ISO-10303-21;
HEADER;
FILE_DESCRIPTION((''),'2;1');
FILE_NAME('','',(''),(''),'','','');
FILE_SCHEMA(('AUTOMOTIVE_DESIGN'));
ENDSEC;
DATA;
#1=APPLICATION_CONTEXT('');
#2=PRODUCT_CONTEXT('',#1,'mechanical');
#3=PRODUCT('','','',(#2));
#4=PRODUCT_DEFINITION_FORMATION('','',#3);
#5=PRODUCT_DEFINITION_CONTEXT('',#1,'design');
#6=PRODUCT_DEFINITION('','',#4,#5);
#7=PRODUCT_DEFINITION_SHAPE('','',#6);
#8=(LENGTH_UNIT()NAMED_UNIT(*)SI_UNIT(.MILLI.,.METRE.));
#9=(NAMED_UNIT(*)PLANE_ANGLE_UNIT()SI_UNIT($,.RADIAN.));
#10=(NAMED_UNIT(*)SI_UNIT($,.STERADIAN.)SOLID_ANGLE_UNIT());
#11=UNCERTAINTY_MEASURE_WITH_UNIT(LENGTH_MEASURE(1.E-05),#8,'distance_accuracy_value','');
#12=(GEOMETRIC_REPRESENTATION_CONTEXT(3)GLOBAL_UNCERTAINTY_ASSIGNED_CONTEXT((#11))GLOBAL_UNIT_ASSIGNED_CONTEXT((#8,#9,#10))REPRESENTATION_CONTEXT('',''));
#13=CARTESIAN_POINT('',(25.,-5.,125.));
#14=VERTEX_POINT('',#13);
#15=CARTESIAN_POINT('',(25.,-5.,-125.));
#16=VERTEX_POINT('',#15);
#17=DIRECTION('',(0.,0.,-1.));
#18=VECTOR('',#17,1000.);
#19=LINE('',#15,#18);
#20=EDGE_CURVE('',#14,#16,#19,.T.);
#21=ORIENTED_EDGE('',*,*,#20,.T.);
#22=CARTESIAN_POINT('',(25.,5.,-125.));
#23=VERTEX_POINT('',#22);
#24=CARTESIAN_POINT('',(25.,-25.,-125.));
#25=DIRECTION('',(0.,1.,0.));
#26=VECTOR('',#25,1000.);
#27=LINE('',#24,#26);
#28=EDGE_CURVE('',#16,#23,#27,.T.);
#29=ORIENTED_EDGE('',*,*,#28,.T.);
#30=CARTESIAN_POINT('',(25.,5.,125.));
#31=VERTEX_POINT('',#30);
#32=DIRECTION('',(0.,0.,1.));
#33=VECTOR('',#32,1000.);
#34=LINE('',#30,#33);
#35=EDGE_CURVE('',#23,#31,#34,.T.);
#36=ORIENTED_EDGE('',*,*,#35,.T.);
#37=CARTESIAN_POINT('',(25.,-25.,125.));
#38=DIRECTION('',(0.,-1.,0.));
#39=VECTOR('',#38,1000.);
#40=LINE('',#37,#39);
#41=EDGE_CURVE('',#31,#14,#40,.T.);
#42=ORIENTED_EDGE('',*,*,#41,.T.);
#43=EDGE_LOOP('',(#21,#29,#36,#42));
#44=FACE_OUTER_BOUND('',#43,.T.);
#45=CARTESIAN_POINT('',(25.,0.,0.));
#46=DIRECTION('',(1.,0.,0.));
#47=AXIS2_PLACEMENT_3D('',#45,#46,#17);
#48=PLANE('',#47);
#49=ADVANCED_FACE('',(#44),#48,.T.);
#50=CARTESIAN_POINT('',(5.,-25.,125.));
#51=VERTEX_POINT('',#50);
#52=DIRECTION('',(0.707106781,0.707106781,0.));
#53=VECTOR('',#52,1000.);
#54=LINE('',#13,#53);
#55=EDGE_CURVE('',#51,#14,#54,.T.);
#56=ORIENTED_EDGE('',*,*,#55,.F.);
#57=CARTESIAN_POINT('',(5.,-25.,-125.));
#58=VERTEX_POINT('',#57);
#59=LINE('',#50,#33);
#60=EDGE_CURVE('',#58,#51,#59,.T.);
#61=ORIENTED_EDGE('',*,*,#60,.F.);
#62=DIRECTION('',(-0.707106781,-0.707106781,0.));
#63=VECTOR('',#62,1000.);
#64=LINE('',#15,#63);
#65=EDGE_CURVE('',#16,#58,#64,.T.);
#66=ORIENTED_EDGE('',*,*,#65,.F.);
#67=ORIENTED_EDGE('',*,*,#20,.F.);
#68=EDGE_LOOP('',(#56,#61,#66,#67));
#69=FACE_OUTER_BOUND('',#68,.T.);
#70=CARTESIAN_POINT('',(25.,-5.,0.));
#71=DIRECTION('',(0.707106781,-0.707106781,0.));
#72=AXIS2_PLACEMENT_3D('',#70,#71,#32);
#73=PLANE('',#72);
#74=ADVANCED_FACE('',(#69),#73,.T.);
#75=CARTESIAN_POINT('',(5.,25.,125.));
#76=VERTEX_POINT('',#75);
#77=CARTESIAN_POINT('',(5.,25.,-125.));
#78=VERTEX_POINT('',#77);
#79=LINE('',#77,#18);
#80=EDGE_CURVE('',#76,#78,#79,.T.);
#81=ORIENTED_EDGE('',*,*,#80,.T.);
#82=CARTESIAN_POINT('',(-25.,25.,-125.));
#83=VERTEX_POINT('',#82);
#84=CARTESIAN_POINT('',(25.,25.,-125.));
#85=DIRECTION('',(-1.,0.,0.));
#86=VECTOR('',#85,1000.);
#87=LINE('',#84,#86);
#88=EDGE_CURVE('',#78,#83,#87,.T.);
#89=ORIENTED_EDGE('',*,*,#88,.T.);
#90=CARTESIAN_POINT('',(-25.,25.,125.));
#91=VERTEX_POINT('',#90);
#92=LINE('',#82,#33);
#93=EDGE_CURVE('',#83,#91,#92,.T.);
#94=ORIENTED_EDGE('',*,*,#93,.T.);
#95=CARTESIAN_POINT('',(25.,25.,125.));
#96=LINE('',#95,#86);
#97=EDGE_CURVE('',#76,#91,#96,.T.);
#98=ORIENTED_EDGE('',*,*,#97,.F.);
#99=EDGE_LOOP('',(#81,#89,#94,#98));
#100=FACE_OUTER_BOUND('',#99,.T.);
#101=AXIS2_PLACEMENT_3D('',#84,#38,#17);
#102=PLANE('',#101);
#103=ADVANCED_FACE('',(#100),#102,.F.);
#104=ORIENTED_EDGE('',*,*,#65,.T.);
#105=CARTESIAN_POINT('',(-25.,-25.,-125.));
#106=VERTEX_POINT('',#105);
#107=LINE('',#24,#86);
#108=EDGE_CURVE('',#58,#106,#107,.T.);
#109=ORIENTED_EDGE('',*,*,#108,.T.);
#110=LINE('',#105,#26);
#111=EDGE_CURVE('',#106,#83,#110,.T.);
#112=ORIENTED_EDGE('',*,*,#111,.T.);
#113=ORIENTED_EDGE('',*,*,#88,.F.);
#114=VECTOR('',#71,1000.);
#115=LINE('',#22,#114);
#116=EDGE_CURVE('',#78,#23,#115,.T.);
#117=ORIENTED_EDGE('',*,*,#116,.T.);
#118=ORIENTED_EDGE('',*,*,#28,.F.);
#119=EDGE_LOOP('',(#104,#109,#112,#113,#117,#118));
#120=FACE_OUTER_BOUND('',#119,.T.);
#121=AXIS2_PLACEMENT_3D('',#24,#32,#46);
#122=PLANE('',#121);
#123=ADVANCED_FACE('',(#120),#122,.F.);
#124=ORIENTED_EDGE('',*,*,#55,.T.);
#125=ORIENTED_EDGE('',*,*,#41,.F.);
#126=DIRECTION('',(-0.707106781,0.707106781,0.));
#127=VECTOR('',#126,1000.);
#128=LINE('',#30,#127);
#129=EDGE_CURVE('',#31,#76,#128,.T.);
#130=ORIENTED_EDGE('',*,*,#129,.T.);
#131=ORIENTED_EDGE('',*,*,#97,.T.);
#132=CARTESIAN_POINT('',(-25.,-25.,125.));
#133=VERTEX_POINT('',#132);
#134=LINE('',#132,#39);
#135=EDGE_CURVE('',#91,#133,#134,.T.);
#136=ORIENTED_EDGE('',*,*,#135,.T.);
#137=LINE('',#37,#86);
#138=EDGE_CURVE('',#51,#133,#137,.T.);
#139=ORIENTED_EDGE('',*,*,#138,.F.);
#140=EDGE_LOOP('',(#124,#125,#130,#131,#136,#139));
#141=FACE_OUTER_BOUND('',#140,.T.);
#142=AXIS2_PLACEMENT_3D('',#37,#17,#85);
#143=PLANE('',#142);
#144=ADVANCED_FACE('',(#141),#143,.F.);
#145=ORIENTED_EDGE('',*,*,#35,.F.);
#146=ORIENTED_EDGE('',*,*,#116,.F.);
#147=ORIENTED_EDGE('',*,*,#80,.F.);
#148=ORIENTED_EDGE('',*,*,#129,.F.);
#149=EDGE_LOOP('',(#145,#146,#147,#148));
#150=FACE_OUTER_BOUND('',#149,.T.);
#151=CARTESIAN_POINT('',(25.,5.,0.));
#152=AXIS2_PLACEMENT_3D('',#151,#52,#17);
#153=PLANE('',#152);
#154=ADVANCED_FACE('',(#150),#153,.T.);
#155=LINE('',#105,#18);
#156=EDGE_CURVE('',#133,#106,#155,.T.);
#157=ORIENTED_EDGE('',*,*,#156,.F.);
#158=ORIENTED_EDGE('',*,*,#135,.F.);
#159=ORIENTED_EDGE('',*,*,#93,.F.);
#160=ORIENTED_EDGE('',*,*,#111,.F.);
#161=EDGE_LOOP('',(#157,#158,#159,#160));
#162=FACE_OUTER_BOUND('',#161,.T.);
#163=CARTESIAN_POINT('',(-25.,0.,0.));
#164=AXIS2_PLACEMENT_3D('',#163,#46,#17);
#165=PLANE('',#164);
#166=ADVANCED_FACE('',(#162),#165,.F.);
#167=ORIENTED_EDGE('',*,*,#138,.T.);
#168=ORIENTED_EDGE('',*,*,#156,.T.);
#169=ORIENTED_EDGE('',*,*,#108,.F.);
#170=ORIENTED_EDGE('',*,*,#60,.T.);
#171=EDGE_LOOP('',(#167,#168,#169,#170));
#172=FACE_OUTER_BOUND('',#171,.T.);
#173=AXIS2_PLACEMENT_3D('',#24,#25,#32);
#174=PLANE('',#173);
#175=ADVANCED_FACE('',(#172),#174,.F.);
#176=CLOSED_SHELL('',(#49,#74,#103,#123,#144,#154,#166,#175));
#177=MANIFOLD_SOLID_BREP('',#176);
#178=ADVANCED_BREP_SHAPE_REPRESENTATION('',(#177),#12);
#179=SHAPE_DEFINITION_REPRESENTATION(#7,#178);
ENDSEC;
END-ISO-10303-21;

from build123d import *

# Parameters (mm, degrees)
SKETCH1_W           = 250
SKETCH1_H           = 50
BOSS_EXTRUDE1_DEPTH = 25
CHAMFER1_SIZE       = 20


with BuildPart() as part:
    # Sketch1 → Boss-Extrude1 (new, symmetric)
    with BuildSketch(Plane(origin=(0, 0, 0), x_dir=(0, 0, -1), z_dir=(1, 0, 0))):
        Rectangle(SKETCH1_W, SKETCH1_H)
    extrude(amount=BOSS_EXTRUDE1_DEPTH, both=True)

    # Chamfer1
    chamfer1_edges = [part.edges().sort_by_distance(p)[0] for p in [
        (25, 25, 0),
        (25, -25, 0),
    ]]
    chamfer(chamfer1_edges, length=CHAMFER1_SIZE)


solid = part.part
